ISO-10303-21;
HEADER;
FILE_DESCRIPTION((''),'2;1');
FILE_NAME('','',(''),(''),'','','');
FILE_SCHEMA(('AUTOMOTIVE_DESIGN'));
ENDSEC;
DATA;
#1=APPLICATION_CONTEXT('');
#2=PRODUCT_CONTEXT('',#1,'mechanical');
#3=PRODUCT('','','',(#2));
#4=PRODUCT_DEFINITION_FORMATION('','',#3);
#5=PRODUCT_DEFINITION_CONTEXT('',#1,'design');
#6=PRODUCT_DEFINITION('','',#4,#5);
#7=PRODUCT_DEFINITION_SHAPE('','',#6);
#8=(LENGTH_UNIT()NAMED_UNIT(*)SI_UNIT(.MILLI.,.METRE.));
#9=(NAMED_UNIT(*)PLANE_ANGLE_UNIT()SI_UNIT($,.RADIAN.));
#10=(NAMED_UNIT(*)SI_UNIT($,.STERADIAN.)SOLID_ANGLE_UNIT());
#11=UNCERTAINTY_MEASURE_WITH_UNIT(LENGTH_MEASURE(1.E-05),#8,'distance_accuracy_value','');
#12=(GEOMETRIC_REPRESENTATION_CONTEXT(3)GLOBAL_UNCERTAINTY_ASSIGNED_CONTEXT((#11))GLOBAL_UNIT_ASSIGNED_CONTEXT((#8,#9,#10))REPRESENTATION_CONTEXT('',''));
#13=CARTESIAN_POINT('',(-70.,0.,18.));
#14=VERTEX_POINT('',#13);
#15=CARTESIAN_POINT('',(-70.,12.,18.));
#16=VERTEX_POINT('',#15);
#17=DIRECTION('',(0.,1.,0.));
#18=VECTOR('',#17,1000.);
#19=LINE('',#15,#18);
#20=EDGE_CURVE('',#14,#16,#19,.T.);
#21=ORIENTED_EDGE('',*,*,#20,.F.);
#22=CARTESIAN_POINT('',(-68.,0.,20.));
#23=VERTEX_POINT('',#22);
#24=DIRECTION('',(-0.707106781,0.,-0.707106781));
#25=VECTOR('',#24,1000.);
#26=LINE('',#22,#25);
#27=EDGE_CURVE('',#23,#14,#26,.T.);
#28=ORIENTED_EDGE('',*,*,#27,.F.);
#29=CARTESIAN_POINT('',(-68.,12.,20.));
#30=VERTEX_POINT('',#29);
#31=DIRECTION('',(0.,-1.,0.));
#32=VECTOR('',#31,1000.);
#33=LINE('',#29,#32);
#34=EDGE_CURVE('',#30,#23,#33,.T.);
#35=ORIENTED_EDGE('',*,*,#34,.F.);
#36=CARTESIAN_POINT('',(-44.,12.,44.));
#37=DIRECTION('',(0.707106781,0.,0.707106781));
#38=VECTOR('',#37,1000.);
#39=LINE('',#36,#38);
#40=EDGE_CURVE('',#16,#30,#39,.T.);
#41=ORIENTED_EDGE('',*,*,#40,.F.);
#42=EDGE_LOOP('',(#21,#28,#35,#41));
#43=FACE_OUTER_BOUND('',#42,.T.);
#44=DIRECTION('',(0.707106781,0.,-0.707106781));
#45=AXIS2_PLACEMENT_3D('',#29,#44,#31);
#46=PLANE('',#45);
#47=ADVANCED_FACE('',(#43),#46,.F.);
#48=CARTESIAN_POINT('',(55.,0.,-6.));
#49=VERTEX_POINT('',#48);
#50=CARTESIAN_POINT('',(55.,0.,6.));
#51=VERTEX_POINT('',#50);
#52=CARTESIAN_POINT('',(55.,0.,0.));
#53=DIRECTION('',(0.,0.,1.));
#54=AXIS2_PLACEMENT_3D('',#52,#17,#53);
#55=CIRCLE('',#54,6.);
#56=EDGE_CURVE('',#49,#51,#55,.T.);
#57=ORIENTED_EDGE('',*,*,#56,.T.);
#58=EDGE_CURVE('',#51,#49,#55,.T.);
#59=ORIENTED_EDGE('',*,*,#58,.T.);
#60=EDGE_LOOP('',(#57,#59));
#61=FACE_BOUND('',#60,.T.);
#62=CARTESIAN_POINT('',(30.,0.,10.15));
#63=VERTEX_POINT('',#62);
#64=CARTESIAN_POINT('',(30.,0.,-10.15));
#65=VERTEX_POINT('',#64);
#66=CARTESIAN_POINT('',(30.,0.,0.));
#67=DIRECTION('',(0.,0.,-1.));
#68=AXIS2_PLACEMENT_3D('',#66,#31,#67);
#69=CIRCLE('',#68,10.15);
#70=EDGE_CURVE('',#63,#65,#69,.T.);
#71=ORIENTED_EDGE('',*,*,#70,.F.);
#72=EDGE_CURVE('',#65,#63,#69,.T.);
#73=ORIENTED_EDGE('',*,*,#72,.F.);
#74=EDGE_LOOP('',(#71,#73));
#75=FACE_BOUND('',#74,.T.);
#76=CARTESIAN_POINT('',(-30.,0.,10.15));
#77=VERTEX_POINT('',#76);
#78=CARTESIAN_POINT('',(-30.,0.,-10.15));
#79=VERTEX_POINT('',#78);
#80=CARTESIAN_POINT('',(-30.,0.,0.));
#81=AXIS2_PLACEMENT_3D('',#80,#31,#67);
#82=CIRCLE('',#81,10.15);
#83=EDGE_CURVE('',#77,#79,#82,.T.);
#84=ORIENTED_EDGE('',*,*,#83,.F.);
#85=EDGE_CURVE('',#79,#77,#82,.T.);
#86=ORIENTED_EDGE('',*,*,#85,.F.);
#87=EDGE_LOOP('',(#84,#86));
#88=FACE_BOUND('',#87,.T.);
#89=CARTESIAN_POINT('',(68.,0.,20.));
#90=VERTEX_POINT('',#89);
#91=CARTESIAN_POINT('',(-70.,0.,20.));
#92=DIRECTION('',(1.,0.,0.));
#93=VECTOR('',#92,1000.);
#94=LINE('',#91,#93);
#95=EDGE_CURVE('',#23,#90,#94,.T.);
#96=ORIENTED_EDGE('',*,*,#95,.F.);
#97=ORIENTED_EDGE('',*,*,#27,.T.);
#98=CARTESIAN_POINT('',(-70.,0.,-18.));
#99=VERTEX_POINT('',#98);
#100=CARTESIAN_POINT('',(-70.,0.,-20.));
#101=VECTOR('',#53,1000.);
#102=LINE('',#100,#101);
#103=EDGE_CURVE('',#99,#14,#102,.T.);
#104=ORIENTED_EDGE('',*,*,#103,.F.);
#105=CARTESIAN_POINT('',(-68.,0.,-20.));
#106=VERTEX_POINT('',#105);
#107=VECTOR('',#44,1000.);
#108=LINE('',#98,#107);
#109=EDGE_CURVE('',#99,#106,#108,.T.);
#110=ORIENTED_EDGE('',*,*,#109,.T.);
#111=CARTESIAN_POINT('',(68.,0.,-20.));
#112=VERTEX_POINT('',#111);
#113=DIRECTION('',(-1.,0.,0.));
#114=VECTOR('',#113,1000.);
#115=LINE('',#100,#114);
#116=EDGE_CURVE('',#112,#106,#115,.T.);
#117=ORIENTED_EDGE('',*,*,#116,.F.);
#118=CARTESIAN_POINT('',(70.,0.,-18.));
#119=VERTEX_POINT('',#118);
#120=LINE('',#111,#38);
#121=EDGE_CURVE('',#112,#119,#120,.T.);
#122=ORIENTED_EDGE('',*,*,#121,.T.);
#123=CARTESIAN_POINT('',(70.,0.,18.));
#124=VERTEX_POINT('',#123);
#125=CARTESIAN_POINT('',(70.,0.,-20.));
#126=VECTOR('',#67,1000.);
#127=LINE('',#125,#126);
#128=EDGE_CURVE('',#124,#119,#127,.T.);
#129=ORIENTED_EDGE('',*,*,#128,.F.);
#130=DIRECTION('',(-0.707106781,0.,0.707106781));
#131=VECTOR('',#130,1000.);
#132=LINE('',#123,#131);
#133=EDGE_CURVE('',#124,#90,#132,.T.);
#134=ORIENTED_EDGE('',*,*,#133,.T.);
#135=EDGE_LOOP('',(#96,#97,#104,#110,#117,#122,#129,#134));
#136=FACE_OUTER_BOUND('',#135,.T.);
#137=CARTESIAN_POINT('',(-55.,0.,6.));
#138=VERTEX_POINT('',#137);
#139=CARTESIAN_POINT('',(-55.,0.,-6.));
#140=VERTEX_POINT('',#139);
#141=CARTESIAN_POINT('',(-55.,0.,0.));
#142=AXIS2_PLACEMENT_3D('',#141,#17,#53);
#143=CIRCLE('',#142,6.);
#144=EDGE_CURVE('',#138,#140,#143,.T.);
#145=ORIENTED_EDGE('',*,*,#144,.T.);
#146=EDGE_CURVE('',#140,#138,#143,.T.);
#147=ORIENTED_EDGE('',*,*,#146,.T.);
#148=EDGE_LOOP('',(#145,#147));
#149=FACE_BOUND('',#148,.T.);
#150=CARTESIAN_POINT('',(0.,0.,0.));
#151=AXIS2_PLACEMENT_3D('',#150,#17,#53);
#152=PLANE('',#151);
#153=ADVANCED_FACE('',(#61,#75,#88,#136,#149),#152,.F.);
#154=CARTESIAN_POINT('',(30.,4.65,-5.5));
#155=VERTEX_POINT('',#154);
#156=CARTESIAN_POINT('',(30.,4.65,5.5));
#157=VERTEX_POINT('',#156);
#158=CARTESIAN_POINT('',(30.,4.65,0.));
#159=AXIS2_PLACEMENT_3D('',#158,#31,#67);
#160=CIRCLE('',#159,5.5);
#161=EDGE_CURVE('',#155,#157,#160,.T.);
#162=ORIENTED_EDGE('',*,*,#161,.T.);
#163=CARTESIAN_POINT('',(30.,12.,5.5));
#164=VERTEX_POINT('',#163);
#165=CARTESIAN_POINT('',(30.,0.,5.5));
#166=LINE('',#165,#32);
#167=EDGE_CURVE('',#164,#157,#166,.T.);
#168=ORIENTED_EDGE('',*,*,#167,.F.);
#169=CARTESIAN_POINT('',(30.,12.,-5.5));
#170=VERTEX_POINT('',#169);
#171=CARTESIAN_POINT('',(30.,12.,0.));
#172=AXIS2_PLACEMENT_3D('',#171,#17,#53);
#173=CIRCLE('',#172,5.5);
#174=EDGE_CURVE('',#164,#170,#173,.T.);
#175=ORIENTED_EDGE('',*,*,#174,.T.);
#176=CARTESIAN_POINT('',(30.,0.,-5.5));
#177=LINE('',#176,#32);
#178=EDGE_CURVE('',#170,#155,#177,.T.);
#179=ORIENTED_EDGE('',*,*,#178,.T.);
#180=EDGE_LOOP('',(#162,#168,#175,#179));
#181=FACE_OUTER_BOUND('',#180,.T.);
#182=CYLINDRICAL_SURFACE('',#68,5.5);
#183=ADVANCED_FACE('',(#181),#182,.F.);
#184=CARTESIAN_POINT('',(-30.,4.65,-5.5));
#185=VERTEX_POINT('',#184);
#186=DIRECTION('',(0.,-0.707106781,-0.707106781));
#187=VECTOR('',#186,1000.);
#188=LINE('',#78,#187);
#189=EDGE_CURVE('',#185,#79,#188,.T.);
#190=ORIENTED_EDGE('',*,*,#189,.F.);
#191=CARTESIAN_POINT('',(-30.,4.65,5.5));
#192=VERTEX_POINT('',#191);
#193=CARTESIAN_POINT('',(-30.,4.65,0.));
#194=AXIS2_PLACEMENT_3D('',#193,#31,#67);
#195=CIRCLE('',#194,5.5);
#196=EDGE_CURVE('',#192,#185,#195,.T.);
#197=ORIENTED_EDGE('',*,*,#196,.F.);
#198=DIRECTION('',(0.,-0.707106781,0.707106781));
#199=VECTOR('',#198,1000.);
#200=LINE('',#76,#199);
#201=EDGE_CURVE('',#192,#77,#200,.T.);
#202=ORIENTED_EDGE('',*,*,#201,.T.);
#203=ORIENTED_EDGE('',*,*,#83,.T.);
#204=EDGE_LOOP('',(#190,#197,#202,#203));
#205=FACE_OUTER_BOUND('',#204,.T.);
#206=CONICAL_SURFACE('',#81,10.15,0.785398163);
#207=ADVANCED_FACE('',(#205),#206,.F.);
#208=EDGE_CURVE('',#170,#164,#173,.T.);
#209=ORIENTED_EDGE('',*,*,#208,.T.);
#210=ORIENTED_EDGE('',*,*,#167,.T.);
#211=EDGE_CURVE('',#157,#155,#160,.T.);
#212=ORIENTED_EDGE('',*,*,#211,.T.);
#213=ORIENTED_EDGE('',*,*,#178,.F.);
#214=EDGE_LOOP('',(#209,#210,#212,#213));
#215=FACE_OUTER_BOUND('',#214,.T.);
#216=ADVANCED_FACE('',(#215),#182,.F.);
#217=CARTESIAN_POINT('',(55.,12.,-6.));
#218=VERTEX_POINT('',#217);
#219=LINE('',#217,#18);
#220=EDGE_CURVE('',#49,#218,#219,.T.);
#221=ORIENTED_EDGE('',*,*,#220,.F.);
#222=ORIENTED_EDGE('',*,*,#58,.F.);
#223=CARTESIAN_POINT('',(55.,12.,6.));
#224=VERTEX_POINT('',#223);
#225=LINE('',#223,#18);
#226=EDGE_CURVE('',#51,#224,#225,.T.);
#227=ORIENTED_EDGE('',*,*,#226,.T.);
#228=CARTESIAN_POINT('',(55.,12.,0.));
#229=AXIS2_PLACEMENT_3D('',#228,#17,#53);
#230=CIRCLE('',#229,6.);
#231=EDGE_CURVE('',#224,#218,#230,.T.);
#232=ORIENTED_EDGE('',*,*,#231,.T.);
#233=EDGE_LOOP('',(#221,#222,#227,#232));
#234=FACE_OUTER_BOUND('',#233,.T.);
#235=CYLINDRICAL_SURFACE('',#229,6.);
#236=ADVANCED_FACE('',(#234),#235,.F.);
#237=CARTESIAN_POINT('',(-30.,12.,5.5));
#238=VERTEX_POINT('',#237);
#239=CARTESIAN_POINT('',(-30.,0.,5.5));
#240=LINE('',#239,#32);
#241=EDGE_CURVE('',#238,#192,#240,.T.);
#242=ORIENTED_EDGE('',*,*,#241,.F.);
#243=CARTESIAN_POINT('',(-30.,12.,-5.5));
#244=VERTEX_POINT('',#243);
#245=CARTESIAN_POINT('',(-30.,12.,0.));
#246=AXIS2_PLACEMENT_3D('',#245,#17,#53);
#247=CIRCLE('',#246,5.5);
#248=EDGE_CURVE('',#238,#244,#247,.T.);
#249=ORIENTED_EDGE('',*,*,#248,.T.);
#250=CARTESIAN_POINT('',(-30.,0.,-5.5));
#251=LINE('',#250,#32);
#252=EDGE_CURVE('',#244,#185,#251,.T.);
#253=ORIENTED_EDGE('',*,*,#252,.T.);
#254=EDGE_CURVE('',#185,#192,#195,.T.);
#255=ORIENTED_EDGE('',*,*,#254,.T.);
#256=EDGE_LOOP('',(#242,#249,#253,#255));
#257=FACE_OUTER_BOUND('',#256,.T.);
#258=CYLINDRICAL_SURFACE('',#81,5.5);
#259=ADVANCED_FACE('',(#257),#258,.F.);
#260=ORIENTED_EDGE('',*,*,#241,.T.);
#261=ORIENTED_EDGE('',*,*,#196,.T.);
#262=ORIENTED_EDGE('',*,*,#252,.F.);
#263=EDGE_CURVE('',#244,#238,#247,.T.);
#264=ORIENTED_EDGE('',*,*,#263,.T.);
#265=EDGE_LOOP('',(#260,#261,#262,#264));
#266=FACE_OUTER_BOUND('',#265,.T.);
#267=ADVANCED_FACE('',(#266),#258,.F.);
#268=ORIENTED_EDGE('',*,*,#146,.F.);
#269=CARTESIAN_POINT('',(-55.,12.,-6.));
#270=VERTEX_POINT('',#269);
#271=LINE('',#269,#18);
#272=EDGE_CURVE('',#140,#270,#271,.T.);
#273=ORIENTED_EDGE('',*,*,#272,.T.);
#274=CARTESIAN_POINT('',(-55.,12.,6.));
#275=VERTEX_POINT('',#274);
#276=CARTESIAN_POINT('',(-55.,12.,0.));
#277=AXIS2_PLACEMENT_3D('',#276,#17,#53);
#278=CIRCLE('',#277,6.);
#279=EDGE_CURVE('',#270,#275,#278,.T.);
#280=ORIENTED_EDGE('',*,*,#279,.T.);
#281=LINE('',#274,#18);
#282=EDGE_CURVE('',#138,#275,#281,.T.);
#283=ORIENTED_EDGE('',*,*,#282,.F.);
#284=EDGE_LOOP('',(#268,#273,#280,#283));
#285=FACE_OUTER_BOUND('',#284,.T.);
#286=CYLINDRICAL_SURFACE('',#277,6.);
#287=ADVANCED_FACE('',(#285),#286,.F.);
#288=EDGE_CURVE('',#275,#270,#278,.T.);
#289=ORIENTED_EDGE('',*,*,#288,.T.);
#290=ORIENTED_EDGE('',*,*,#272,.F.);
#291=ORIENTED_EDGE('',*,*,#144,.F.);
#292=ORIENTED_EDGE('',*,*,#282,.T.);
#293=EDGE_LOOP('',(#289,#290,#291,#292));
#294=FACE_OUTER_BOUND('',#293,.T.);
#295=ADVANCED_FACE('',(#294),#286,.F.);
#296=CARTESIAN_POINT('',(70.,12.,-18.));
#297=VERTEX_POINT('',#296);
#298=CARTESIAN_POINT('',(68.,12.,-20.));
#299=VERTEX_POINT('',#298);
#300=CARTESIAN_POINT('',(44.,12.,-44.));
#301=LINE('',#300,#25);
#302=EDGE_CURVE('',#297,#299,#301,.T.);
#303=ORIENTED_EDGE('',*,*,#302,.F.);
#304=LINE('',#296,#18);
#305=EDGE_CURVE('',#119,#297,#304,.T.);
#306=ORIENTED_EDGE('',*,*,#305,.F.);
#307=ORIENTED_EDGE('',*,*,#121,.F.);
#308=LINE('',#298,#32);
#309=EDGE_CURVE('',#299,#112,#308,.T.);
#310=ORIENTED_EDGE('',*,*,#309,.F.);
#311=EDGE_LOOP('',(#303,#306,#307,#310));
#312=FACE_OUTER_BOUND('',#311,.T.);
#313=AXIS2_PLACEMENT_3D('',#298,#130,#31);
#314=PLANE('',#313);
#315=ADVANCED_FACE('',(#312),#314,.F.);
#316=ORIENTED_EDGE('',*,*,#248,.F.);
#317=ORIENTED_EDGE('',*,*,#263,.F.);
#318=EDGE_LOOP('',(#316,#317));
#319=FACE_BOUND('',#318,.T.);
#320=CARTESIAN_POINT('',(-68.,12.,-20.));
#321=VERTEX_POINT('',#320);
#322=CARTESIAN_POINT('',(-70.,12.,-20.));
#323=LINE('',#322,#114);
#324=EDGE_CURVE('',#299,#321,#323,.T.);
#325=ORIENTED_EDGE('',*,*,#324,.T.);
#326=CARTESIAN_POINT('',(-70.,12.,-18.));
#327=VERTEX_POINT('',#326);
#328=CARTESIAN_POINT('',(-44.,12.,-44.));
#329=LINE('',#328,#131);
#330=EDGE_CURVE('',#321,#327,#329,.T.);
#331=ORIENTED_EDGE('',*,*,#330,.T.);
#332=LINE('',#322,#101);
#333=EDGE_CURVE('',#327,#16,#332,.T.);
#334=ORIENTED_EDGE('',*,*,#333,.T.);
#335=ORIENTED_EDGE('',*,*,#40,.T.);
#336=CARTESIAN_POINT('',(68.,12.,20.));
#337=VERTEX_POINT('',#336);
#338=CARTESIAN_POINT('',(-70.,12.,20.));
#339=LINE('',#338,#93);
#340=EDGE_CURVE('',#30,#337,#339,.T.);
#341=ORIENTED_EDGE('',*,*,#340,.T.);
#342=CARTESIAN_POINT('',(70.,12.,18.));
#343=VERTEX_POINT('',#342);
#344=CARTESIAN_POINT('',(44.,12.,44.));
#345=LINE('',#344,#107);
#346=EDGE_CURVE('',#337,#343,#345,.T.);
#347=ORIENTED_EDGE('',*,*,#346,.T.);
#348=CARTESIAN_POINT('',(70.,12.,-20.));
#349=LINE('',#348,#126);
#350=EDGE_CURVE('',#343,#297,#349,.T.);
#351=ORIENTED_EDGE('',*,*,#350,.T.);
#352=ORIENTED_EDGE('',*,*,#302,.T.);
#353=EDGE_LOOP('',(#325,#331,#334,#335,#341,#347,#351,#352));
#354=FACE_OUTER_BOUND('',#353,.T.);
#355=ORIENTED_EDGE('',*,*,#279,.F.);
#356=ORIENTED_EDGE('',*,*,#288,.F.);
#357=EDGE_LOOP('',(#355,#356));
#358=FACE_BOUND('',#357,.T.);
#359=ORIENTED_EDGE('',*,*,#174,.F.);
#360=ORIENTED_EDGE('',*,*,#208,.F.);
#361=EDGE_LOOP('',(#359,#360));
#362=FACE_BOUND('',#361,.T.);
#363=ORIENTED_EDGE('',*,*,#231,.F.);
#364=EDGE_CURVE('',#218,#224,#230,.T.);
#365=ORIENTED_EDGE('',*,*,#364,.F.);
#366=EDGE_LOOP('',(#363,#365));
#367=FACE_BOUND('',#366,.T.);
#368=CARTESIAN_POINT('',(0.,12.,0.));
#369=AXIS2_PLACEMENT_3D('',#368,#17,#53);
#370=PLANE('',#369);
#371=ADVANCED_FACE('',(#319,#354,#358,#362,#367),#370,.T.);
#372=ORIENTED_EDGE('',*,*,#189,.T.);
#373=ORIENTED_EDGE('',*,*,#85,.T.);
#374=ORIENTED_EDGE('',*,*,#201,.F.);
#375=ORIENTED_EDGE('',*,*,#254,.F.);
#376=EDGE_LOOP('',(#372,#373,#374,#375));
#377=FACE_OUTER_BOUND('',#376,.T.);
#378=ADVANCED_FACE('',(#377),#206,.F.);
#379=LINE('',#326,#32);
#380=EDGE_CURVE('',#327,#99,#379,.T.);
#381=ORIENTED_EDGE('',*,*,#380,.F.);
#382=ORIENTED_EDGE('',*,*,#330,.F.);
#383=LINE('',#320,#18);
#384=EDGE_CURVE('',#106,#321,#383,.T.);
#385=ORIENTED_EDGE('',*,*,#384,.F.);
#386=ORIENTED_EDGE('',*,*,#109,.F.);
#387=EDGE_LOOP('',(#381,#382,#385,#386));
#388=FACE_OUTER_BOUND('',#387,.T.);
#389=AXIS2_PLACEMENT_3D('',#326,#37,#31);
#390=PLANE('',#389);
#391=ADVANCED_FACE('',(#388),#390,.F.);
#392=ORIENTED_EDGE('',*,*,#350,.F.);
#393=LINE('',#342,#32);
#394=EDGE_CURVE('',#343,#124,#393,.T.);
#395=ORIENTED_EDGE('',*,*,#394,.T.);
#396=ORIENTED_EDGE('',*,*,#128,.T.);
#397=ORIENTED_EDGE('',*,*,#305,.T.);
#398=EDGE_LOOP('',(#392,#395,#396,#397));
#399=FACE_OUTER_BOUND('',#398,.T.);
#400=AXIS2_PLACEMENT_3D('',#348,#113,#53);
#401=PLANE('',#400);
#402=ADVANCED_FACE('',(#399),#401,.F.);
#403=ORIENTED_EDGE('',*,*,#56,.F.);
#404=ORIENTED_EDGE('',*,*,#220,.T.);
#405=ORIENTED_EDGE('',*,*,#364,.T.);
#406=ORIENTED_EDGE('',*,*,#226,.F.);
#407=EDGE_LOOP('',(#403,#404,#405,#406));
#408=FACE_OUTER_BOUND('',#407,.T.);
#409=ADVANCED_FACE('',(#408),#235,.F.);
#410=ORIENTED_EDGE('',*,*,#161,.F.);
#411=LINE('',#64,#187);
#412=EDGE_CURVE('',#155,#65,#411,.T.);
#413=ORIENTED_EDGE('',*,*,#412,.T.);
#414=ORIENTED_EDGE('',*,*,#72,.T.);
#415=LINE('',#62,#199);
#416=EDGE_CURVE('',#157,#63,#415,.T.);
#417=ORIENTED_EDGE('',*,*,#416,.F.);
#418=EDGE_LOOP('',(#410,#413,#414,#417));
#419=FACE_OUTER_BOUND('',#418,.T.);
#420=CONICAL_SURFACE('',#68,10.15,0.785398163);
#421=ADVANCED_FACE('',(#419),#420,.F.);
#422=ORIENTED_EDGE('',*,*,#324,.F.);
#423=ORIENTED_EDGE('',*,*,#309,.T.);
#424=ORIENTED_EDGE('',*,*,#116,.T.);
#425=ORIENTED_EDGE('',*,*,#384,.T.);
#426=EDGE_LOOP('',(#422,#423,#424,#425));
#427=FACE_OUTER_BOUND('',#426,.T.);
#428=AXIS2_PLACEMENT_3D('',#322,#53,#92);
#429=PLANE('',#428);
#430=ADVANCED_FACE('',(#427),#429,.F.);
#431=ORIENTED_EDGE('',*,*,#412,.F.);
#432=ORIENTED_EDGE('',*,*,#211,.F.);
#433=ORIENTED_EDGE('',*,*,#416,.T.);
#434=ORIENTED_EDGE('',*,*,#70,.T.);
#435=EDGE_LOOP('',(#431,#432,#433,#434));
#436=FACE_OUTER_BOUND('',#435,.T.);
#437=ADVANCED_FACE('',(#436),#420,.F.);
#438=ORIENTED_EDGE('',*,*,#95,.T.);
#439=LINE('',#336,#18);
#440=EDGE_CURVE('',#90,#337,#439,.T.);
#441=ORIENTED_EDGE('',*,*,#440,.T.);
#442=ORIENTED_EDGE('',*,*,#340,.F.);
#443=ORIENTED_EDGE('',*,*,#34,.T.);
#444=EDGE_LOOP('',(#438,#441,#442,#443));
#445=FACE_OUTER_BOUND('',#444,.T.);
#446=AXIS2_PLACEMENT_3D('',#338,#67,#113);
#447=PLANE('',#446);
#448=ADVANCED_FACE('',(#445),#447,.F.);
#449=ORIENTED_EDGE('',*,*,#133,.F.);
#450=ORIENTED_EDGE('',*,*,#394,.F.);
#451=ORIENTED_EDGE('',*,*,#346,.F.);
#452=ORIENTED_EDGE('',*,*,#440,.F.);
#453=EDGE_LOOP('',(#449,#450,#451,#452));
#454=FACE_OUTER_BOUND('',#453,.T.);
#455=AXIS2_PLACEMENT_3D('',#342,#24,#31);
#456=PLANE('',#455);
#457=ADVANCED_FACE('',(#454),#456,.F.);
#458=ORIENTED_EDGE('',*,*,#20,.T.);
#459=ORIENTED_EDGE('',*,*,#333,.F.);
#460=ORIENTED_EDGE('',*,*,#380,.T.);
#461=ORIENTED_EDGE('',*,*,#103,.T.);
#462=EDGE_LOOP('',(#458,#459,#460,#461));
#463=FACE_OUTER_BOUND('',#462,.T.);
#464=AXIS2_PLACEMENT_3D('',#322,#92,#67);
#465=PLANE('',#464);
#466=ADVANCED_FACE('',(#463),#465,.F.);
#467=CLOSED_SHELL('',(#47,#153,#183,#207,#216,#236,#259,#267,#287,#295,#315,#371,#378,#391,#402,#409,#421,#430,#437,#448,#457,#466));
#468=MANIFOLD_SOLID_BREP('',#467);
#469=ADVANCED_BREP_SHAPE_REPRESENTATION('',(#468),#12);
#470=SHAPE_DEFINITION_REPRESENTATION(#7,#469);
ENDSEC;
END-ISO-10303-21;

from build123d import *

# Parameters (mm, degrees)
SKETCH5_W                                         = 140
SKETCH5_H                                         = 40
BOSS_EXTRUDE1_DEPTH                               = 12
M10_CLEARANCE_HOLE1_D                             = 12
M10_CLEARANCE_HOLE1_DEPTH                         = 53
M10_CLEARANCE_HOLE1_TIP                           = 3.605163714
HOLE_SIZE_BASED_HEX_SOCKET_COUNTERSUN_D           = 11
HOLE_SIZE_BASED_HEX_SOCKET_COUNTERSUN_DEPTH       = 53
HOLE_SIZE_BASED_HEX_SOCKET_COUNTERSUN_CSINK_D     = 20.3
HOLE_SIZE_BASED_HEX_SOCKET_COUNTERSUN_CSINK_ANGLE = 90
HOLE_SIZE_BASED_HEX_SOCKET_COUNTERSUN_TIP         = 3.304733405
CHAMFER1_SIZE                                     = 2


with BuildPart() as part:
    # Sketch5 → Boss-Extrude1 (new body)
    with BuildSketch(Plane(origin=(0, 0, 0), x_dir=(1, 0, 0), z_dir=(0, 1, 0))):
        Rectangle(SKETCH5_W, SKETCH5_H)
    extrude(amount=BOSS_EXTRUDE1_DEPTH)

    # M10 Clearance Hole1
    with Locations(Plane(origin=(0, 12, 0), x_dir=(1, 0, 0), z_dir=(0, 1, 0))):
        with Locations((-55, 0), (55, 0)):
            Hole(M10_CLEARANCE_HOLE1_D / 2, depth=M10_CLEARANCE_HOLE1_DEPTH)
            with Locations((0, 0, -(M10_CLEARANCE_HOLE1_DEPTH + M10_CLEARANCE_HOLE1_TIP / 2))):  # 118° drill point
                Cone(0, M10_CLEARANCE_HOLE1_D / 2, M10_CLEARANCE_HOLE1_TIP, mode=Mode.SUBTRACT)

    # Hole size (%-based) hex socket countersunk screw type2
    with Locations(Plane(origin=(0, 0, 0), x_dir=(-1, 0, 0), z_dir=(0, -1, 0))):
        with Locations((-30, 0), (30, 0)):
            CounterSinkHole(HOLE_SIZE_BASED_HEX_SOCKET_COUNTERSUN_D / 2, HOLE_SIZE_BASED_HEX_SOCKET_COUNTERSUN_CSINK_D / 2, depth=HOLE_SIZE_BASED_HEX_SOCKET_COUNTERSUN_DEPTH, counter_sink_angle=HOLE_SIZE_BASED_HEX_SOCKET_COUNTERSUN_CSINK_ANGLE)
            with Locations((0, 0, -(HOLE_SIZE_BASED_HEX_SOCKET_COUNTERSUN_DEPTH + HOLE_SIZE_BASED_HEX_SOCKET_COUNTERSUN_TIP / 2))):  # 118° drill point
                Cone(0, HOLE_SIZE_BASED_HEX_SOCKET_COUNTERSUN_D / 2, HOLE_SIZE_BASED_HEX_SOCKET_COUNTERSUN_TIP, mode=Mode.SUBTRACT)

    # Chamfer1
    chamfer1_edges = [part.edges().sort_by_distance(p)[0] for p in [
        (70, 6, 20),
        (-70, 6, 20),
        (-70, 6, -20),
        (70, 6, -20),
    ]]
    chamfer(chamfer1_edges, length=CHAMFER1_SIZE)


solid = part.part
